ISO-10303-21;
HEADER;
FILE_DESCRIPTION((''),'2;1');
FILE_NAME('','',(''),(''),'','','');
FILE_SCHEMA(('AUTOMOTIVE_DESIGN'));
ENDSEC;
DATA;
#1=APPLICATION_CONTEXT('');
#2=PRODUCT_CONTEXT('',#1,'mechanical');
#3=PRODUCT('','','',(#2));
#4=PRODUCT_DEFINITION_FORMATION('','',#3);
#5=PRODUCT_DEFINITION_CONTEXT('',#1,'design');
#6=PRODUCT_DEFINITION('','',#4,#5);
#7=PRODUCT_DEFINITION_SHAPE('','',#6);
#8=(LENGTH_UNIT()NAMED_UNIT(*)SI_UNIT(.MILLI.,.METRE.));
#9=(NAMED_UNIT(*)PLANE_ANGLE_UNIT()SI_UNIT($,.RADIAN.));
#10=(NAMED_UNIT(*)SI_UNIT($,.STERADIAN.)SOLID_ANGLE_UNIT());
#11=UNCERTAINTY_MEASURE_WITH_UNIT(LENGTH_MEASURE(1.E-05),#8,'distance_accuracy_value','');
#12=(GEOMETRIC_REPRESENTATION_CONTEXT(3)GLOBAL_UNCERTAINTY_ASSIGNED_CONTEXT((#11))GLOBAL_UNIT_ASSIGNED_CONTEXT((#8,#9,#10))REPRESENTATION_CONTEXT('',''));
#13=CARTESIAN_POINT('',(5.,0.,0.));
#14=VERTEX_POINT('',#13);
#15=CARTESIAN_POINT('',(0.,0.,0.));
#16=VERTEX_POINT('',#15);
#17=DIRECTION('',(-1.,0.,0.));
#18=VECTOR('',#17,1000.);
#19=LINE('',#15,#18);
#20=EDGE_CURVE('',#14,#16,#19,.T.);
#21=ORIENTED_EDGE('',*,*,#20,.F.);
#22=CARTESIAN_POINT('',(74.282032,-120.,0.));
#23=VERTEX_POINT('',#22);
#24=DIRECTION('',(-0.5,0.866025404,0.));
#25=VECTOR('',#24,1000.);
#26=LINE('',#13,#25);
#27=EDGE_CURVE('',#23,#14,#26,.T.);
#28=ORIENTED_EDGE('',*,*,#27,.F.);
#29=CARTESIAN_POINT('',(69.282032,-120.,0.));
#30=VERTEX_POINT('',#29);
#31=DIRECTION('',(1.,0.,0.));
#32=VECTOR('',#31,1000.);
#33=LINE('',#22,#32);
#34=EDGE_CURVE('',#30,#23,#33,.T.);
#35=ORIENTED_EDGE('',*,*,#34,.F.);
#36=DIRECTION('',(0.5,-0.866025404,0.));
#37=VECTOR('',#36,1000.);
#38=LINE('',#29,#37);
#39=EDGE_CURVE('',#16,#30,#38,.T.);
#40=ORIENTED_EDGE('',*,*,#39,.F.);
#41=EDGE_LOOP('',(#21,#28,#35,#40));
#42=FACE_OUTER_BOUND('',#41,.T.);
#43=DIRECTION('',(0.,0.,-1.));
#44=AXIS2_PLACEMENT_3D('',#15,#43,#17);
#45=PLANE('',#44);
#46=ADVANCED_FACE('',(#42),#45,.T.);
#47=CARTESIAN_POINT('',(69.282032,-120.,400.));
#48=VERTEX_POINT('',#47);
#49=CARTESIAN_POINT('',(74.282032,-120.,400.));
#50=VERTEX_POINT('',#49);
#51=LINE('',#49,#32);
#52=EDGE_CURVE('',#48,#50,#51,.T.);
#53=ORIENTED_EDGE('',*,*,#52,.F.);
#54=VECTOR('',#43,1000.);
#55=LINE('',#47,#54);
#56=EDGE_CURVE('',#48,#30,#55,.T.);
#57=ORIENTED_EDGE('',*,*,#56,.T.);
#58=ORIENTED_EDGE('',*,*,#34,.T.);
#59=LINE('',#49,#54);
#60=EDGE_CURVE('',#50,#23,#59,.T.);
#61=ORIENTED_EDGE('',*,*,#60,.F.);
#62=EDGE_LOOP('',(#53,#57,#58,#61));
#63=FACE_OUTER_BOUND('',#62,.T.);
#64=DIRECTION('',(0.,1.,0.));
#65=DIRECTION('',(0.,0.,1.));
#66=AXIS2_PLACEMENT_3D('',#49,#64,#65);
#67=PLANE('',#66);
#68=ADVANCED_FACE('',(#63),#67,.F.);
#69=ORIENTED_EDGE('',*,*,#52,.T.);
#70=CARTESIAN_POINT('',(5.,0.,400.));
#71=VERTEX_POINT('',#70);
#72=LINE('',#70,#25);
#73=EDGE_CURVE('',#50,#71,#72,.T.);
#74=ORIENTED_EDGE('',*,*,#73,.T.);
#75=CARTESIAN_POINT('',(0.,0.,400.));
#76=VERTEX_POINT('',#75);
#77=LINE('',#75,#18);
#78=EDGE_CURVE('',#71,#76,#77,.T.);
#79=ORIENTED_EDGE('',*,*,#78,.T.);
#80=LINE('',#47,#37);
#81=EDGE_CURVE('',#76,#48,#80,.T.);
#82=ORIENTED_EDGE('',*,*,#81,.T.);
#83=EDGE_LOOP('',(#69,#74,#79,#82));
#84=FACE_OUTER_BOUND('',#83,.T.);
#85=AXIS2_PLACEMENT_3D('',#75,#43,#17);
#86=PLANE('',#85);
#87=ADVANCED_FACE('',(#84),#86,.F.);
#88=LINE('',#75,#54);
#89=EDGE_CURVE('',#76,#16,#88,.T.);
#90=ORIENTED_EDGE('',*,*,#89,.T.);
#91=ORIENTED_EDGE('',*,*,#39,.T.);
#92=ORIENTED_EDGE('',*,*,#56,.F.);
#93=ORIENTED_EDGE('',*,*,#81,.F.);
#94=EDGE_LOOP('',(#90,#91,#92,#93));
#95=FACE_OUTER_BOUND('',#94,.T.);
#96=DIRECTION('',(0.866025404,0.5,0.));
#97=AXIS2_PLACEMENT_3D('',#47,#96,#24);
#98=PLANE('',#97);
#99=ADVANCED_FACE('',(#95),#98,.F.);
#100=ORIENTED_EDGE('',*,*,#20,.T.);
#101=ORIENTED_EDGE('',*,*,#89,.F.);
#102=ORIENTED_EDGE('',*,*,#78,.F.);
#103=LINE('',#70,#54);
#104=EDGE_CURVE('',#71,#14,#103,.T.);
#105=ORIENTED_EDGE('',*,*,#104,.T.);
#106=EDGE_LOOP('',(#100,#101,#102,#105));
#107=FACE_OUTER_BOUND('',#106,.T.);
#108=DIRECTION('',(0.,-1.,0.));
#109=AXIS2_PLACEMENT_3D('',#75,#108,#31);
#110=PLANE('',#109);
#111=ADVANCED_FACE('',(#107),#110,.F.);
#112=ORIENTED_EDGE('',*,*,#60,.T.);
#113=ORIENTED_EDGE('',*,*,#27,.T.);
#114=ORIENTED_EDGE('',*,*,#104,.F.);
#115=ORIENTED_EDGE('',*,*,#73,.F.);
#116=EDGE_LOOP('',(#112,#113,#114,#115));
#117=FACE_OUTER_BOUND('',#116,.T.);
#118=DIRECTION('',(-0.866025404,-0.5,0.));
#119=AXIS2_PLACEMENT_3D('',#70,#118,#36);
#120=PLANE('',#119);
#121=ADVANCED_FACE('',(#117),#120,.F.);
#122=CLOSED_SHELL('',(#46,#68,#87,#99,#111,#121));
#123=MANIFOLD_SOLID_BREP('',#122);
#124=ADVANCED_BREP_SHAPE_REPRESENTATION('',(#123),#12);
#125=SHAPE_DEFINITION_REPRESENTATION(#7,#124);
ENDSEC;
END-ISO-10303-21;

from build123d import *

# Parameters (mm, degrees)
EXTRUDE_1_DEPTH = 400


with BuildPart() as part:
    # 草图1 → 凸台-拉伸1 (new body)
    with BuildSketch(Plane.XY):
        Polygon((0, 0), (5, 0), (74.282032303, -120), (69.282032303, -120), align=None)
    extrude(amount=EXTRUDE_1_DEPTH)


solid = part.part
